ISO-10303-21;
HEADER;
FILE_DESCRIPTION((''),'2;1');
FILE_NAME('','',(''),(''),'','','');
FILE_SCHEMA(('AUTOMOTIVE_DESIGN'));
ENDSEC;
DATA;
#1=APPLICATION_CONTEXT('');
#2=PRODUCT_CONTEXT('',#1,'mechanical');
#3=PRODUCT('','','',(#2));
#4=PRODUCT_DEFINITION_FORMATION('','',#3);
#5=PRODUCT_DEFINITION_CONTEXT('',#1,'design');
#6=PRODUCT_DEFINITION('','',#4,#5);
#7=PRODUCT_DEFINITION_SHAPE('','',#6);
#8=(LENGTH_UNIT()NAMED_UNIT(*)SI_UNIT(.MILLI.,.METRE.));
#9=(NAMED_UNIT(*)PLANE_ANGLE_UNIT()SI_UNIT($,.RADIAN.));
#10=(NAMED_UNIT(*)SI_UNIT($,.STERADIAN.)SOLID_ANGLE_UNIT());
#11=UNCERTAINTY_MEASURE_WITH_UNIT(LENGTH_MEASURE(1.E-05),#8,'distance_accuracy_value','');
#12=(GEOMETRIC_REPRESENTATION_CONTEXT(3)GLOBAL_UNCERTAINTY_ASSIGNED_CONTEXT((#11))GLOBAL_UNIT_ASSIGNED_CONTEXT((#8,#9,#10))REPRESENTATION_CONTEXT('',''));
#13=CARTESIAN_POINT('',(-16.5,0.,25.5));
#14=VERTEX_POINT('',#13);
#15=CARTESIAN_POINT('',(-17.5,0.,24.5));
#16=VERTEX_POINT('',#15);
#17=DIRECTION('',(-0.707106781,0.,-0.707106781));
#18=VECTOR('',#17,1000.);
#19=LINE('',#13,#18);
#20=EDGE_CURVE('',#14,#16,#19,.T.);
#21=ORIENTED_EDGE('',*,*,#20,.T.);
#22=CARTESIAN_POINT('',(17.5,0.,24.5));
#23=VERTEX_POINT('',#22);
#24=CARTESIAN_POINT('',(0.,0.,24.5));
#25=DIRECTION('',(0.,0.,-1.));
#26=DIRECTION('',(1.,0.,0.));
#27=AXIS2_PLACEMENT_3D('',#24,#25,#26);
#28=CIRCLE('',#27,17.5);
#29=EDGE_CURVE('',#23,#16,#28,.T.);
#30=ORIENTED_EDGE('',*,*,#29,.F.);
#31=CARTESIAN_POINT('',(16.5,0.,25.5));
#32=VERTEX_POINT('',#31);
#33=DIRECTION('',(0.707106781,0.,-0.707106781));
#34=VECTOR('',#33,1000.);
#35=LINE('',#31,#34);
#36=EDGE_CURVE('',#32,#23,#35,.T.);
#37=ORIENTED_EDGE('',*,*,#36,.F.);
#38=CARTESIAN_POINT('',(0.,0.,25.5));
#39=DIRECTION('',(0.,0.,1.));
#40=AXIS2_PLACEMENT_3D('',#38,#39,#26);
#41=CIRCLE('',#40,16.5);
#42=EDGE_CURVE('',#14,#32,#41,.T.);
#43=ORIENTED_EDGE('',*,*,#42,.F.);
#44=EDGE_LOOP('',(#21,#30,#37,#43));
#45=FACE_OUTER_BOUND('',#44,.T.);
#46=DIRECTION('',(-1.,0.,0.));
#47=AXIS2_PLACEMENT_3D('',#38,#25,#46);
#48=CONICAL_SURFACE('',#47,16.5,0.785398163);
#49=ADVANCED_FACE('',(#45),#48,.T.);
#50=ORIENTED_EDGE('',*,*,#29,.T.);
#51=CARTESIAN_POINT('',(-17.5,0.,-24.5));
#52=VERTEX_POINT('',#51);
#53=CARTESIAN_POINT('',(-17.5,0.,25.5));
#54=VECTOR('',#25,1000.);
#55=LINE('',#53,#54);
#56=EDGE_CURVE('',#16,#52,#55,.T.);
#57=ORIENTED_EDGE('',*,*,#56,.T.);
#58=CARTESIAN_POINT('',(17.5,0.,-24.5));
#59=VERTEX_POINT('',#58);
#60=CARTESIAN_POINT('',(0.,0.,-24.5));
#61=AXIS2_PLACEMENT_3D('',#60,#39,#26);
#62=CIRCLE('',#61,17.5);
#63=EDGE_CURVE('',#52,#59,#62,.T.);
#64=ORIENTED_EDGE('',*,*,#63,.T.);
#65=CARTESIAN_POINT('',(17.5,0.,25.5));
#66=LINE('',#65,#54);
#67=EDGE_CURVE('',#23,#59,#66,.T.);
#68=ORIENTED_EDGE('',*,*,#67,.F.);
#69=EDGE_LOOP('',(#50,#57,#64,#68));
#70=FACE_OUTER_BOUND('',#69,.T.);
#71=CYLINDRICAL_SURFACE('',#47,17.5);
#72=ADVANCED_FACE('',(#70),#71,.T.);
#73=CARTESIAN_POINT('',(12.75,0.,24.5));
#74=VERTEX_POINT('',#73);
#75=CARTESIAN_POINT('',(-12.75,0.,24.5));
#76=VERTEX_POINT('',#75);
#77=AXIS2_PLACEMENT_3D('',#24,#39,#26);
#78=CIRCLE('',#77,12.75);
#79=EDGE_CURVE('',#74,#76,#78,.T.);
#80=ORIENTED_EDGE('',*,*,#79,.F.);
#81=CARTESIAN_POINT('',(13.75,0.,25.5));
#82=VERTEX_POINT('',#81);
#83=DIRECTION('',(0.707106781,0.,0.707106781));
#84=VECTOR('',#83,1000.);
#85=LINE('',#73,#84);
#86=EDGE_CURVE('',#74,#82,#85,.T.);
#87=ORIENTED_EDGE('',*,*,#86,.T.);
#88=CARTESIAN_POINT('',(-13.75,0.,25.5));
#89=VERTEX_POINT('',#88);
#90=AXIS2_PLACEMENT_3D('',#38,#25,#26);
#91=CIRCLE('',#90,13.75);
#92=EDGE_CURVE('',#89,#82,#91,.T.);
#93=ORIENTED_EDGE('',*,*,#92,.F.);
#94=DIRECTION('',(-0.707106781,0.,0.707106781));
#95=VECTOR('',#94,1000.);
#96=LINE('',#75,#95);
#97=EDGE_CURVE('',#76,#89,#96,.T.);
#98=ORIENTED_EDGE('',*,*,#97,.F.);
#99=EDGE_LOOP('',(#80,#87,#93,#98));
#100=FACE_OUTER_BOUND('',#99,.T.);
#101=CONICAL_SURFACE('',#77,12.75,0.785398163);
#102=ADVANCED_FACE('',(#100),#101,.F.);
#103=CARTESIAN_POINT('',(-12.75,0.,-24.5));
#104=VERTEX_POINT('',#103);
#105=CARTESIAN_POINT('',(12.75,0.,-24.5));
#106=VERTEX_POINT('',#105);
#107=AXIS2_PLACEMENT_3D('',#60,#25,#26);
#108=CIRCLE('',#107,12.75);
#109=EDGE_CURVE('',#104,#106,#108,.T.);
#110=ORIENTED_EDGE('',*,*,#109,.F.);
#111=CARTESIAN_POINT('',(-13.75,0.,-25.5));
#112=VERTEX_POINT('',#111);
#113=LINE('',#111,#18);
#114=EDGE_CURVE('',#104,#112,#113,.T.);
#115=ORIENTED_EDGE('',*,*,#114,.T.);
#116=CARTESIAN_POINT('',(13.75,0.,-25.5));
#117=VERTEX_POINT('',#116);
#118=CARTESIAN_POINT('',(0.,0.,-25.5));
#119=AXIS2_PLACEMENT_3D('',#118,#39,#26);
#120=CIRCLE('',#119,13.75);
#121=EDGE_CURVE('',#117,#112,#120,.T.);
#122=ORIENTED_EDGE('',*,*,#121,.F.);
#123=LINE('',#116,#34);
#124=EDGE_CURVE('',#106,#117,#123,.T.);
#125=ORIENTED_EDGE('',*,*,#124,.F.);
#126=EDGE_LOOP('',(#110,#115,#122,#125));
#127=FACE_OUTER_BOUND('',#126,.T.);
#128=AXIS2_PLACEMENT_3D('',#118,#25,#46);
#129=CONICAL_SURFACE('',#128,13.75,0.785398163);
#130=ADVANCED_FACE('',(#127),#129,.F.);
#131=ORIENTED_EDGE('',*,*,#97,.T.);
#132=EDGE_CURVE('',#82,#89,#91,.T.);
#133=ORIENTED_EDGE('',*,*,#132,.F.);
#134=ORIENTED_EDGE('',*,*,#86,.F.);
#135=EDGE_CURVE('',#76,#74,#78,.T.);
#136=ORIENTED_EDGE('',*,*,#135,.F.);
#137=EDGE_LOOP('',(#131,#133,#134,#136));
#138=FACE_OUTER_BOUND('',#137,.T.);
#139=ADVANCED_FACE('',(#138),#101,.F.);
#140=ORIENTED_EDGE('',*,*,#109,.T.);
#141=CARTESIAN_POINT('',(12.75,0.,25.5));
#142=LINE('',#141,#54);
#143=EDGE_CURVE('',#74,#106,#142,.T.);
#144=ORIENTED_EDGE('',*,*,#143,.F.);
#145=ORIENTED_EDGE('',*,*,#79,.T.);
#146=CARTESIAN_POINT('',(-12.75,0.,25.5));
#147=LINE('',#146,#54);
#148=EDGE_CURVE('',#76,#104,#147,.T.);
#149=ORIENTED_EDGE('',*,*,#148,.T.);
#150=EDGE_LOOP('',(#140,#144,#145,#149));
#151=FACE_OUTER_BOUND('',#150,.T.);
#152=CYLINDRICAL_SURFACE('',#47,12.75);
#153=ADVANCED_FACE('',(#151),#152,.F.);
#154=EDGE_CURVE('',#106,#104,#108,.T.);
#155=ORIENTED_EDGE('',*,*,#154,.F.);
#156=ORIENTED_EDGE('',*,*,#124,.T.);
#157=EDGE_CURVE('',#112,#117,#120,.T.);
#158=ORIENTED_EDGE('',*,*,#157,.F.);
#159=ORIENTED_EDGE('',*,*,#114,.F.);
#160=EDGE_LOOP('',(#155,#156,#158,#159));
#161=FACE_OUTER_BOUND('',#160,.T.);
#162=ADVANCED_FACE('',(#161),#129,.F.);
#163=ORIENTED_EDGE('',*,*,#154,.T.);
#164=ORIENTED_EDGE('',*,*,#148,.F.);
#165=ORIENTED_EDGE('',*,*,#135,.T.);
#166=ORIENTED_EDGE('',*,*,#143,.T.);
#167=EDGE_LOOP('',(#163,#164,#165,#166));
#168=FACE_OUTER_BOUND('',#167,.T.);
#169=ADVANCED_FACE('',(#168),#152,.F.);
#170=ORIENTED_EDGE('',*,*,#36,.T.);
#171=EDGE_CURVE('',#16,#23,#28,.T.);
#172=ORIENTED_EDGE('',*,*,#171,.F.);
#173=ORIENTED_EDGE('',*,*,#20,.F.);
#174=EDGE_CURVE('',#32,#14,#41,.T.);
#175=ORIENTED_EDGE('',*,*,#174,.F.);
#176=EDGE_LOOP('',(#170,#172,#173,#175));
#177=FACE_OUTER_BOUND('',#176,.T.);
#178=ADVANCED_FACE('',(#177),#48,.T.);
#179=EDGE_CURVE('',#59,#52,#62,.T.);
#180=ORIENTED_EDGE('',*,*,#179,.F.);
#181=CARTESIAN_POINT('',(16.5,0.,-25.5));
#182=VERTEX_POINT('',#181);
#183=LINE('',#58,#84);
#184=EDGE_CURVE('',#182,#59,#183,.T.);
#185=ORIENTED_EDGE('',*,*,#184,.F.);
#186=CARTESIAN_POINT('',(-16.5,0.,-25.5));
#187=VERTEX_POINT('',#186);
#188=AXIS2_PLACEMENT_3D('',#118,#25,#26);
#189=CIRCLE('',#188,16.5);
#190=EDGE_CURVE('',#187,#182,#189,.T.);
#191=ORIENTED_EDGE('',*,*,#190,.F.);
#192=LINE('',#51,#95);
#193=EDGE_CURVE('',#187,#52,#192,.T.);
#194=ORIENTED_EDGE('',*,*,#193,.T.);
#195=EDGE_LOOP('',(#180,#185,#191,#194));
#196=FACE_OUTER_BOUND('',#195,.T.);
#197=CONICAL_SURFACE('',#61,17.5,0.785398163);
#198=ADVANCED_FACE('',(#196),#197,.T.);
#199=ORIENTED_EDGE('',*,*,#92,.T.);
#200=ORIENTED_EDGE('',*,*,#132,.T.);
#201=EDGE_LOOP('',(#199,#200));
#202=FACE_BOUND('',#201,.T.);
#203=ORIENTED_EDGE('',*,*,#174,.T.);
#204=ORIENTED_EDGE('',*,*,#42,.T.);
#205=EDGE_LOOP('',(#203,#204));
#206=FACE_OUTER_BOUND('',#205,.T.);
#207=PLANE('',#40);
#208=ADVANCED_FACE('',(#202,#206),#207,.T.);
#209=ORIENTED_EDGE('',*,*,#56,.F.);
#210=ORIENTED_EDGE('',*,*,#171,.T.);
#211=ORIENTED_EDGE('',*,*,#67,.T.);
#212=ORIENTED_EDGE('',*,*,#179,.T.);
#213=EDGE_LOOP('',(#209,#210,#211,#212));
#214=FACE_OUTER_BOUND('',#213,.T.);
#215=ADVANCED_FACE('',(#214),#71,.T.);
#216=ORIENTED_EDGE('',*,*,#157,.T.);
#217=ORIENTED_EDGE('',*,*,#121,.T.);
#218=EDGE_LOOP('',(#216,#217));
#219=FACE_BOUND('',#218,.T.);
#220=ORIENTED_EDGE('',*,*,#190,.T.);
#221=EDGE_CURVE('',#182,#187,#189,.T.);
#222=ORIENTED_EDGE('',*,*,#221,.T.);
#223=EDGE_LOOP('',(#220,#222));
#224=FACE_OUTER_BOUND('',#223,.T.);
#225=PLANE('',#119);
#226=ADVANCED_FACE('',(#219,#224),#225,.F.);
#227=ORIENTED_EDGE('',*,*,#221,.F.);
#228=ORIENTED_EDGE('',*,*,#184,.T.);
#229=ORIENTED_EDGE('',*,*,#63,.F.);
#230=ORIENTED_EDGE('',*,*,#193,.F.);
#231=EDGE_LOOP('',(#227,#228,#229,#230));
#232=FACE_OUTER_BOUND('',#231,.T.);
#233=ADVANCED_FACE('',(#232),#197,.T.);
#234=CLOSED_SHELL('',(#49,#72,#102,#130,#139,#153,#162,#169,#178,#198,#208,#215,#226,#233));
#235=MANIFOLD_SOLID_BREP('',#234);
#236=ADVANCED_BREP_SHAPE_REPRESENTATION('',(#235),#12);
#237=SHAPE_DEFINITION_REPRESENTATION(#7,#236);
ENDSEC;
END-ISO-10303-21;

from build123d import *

# Parameters (mm, degrees)
SKETCH_1_R      = 17.5
SKETCH_1_R_2    = 12.75
EXTRUDE_1_DEPTH = 25.5
CHAMFER_1_SIZE  = 1


with BuildPart() as part:
    # 草图1 → 凸台-拉伸1 (new, symmetric)
    with BuildSketch(Plane.XY):
        Circle(SKETCH_1_R)
        Circle(SKETCH_1_R_2, mode=Mode.SUBTRACT)
    extrude(amount=EXTRUDE_1_DEPTH, both=True)

    # 倒角1
    chamfer_1_edges = [part.edges().sort_by_distance(p)[0] for p in [
        (-17.5, 0, -25.5),
        (-17.5, 0, 25.5),
        (-12.75, 0, -25.5),
        (-12.75, 0, 25.5),
    ]]
    chamfer(chamfer_1_edges, length=CHAMFER_1_SIZE)


solid = part.part
